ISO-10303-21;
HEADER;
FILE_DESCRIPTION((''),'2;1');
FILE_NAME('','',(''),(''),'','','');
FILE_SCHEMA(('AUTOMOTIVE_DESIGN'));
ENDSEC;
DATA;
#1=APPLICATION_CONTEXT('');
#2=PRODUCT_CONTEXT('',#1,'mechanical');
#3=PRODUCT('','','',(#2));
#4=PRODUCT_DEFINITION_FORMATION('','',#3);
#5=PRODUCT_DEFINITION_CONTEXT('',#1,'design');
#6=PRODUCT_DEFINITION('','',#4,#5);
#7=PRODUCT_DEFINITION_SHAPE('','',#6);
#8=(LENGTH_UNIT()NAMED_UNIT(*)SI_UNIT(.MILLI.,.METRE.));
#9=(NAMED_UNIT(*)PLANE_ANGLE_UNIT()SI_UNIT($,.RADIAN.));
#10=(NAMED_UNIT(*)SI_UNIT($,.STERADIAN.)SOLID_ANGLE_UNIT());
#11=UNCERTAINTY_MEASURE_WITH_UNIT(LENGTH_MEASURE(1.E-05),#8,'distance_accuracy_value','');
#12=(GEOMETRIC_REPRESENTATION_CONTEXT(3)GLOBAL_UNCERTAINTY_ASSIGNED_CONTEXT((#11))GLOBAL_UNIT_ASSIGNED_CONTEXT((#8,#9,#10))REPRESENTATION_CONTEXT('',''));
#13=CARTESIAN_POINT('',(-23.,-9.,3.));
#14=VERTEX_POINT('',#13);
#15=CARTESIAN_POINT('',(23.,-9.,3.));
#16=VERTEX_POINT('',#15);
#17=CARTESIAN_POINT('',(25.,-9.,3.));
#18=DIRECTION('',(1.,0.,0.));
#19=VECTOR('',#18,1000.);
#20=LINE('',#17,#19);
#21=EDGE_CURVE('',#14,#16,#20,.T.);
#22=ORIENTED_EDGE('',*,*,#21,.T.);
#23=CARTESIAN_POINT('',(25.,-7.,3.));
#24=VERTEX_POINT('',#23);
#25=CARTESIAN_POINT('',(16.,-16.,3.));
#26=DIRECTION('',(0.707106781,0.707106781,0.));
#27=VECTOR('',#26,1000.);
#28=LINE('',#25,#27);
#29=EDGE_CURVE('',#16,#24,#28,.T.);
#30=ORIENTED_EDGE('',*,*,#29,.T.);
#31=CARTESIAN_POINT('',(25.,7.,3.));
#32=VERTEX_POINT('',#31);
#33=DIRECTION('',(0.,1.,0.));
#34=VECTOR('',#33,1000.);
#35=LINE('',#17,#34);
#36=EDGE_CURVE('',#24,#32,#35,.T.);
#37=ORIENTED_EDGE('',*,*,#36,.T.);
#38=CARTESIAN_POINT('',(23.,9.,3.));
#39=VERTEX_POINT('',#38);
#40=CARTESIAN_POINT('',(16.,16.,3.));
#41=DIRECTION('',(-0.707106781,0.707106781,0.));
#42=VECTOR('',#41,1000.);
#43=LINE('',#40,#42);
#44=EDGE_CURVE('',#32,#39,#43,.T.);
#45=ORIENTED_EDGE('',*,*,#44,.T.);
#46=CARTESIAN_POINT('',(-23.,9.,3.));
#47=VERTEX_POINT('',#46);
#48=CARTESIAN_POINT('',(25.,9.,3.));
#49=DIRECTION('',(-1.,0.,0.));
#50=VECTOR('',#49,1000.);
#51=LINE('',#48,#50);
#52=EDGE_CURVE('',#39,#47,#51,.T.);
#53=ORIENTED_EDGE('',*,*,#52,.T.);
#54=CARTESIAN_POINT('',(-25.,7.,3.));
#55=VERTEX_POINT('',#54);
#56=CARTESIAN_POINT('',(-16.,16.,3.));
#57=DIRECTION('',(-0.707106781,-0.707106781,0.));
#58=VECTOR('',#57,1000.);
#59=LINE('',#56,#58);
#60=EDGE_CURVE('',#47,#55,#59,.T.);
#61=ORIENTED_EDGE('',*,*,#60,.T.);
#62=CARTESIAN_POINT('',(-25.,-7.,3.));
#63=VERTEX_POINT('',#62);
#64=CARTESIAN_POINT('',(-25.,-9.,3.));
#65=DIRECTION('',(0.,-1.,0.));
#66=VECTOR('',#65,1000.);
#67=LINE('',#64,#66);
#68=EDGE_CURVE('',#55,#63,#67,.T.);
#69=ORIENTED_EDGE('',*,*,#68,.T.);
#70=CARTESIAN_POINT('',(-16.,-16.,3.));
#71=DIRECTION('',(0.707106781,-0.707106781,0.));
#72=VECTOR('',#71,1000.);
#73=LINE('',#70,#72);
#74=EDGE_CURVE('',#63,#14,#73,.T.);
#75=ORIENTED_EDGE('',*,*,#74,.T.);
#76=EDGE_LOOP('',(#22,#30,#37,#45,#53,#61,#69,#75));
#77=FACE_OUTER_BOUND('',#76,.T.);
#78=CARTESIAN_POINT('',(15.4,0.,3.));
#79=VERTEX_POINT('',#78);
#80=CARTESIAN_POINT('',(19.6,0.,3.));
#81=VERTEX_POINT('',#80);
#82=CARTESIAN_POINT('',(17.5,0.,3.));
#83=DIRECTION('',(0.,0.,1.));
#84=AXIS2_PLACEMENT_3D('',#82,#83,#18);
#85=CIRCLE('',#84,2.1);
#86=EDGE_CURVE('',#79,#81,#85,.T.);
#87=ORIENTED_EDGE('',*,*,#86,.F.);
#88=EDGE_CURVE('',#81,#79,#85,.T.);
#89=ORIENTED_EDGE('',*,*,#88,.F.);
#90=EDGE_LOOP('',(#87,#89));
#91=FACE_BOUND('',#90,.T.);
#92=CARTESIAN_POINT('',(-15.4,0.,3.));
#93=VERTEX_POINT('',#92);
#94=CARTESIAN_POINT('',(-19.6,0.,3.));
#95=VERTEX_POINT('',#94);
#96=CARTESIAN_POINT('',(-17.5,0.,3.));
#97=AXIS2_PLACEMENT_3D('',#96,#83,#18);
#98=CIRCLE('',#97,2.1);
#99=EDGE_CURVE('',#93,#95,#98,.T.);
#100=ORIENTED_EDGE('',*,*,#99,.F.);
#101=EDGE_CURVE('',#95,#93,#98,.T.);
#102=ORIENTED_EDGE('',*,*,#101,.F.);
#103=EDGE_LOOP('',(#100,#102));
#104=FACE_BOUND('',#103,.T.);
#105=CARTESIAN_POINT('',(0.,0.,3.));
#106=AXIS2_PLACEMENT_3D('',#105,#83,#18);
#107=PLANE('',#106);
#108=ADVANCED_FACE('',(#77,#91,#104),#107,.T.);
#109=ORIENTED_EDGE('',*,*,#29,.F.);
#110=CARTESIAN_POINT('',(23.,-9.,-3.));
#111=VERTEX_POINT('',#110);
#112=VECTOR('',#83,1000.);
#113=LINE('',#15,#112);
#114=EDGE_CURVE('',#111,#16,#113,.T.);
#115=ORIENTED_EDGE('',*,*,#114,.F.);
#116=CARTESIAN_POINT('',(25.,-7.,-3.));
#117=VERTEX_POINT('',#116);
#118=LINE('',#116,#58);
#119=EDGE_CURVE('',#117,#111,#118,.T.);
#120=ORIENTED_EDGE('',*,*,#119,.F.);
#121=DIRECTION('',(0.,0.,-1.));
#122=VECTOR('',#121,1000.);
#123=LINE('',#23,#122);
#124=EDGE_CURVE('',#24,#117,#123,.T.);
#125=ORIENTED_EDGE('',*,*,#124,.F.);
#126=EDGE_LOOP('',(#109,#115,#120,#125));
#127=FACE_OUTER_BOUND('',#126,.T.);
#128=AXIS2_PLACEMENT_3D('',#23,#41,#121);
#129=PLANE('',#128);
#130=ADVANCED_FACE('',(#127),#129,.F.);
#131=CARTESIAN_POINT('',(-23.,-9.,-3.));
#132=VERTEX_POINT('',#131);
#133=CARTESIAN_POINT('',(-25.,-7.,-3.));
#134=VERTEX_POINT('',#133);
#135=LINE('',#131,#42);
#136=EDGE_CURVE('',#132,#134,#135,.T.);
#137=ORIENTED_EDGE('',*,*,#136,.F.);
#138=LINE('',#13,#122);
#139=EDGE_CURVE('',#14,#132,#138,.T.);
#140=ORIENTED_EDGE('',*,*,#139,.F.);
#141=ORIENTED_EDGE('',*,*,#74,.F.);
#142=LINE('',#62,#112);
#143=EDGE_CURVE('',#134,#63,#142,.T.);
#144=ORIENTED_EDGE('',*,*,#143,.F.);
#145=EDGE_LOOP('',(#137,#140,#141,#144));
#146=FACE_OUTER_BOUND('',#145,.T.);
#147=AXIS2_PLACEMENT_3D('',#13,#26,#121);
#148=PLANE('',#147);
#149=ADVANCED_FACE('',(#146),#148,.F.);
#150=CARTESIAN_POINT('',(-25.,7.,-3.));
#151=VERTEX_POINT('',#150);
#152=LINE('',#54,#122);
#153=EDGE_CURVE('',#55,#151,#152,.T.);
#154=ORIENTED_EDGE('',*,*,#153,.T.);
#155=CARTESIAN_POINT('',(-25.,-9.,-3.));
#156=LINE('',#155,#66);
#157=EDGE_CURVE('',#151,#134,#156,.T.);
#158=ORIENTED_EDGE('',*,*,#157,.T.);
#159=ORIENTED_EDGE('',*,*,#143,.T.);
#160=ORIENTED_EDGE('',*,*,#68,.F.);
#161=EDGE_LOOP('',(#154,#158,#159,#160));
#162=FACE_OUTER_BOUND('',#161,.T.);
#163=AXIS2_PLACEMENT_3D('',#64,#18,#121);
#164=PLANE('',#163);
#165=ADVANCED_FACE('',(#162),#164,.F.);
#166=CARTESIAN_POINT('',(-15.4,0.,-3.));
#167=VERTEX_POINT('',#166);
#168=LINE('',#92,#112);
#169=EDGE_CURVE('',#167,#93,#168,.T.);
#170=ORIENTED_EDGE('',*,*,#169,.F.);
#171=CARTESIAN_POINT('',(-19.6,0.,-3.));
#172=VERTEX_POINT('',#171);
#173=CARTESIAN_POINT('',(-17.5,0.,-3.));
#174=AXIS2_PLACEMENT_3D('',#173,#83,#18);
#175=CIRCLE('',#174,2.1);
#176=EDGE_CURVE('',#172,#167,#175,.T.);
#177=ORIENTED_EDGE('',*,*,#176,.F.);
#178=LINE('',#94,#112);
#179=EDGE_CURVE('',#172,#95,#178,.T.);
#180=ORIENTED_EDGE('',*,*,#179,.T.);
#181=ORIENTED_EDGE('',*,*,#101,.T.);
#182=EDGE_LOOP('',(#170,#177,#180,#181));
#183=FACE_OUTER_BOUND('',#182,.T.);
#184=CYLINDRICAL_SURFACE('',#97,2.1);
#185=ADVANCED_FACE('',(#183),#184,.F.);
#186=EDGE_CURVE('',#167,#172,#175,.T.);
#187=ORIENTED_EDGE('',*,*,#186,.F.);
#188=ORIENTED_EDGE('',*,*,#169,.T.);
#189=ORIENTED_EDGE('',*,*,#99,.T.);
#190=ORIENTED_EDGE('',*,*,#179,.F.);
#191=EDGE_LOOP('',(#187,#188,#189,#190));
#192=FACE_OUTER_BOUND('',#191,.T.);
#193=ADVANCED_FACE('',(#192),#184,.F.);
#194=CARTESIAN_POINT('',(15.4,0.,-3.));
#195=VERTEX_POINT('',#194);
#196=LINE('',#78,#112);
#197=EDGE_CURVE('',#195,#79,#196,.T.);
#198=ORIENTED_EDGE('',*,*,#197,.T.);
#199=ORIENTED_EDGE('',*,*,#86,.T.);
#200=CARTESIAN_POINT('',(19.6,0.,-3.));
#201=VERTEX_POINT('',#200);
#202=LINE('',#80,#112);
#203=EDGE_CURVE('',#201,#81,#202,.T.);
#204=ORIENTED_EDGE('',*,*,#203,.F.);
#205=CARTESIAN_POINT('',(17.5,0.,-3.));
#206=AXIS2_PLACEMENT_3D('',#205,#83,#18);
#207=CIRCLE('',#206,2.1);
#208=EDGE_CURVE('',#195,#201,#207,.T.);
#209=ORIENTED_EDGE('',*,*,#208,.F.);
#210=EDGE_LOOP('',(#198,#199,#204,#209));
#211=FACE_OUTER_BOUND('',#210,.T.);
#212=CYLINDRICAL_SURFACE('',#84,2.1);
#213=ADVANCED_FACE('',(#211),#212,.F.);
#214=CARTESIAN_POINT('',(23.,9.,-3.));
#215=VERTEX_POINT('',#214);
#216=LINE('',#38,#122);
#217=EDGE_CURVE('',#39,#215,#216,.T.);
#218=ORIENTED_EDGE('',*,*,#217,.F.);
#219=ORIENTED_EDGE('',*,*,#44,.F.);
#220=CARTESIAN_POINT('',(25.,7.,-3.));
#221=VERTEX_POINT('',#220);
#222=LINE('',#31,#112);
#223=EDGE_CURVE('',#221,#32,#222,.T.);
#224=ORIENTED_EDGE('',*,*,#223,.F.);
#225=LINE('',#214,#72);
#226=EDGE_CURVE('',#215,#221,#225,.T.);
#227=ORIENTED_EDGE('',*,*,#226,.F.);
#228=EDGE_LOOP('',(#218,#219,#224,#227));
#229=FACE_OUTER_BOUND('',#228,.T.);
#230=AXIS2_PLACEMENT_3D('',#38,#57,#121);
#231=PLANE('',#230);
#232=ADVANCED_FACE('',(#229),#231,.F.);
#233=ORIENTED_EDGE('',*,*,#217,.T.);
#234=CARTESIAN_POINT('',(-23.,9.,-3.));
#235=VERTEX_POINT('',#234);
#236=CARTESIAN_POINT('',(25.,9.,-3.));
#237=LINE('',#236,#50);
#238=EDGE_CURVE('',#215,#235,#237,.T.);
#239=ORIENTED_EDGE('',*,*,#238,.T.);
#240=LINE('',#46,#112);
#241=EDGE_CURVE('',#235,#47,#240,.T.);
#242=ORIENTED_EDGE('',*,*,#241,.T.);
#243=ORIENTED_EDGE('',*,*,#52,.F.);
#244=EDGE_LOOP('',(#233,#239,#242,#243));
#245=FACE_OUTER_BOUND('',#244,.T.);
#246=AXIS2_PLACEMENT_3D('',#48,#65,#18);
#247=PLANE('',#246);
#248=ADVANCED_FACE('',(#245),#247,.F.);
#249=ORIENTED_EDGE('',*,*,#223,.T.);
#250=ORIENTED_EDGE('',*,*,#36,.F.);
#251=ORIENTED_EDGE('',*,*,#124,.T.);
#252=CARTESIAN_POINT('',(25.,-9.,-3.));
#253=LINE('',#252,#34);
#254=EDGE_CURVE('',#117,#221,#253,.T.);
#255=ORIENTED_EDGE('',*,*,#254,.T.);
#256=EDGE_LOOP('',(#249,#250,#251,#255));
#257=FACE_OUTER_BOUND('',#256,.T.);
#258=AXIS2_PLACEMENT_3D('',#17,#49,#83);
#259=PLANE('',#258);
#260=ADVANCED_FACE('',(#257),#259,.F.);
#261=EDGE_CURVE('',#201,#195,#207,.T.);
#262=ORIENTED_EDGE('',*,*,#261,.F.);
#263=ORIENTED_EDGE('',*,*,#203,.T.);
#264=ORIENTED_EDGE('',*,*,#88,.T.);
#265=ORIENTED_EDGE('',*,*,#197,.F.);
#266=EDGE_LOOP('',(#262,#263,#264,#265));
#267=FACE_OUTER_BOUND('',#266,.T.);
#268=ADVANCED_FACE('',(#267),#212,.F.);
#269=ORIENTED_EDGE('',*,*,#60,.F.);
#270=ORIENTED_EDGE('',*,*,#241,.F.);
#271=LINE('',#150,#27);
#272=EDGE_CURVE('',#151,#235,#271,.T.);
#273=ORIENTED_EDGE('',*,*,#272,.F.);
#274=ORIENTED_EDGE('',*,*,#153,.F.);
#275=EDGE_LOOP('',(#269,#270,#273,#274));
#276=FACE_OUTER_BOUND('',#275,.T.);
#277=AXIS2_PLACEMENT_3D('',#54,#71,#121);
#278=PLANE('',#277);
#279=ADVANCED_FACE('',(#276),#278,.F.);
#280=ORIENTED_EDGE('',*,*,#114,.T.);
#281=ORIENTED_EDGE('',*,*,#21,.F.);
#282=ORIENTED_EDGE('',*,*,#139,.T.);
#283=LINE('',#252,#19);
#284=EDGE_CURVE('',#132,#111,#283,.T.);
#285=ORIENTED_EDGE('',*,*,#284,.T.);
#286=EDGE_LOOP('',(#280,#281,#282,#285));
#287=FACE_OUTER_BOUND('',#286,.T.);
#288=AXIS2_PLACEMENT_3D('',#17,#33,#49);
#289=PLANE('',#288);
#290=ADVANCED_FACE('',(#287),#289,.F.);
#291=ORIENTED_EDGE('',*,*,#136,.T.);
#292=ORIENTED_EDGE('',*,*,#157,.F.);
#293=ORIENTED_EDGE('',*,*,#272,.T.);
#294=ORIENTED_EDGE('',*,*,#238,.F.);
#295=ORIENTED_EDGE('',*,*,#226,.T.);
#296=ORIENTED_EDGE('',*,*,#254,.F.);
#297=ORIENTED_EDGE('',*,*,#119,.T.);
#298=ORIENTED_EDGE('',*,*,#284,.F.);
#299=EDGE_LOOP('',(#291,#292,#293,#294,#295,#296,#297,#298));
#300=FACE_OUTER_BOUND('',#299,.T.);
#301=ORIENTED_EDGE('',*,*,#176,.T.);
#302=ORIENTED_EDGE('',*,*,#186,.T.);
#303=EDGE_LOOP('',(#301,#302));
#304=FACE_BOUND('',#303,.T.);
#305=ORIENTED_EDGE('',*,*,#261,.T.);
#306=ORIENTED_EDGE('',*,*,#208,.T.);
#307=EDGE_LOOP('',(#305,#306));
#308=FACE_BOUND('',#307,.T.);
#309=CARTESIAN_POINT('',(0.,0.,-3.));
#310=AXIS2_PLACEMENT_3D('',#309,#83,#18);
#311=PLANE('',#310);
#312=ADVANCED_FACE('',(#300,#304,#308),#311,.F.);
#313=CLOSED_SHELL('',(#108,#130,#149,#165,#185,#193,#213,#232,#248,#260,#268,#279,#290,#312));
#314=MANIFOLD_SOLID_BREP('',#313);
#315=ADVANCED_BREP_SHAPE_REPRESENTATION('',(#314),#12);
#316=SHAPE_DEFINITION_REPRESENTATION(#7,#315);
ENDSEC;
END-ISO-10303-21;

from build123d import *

# Parameters (mm, degrees)
SKETCH1_W           = 50
SKETCH1_H           = 18
BOSS_EXTRUDE1_DEPTH = 3
M5_TAPPED_HOLE1_D   = 4.2
CHAMFER1_SIZE       = 2


with BuildPart() as part:
    # Sketch1 → Boss-Extrude1 (new, symmetric)
    with BuildSketch(Plane.XY):
        Rectangle(SKETCH1_W, SKETCH1_H)
    extrude(amount=BOSS_EXTRUDE1_DEPTH, both=True)

    # M5 Tapped Hole1 (through all)
    with Locations(Plane.XY.offset(3)):
        with Locations((-17.5, 0), (17.5, 0)):
            Hole(M5_TAPPED_HOLE1_D / 2)

    # Chamfer1
    chamfer1_edges = [part.edges().sort_by_distance(p)[0] for p in [
        (-25, 9, 0),
        (25, 9, 0),
        (25, -9, 0),
        (-25, -9, 0),
    ]]
    chamfer(chamfer1_edges, length=CHAMFER1_SIZE)


solid = part.part
